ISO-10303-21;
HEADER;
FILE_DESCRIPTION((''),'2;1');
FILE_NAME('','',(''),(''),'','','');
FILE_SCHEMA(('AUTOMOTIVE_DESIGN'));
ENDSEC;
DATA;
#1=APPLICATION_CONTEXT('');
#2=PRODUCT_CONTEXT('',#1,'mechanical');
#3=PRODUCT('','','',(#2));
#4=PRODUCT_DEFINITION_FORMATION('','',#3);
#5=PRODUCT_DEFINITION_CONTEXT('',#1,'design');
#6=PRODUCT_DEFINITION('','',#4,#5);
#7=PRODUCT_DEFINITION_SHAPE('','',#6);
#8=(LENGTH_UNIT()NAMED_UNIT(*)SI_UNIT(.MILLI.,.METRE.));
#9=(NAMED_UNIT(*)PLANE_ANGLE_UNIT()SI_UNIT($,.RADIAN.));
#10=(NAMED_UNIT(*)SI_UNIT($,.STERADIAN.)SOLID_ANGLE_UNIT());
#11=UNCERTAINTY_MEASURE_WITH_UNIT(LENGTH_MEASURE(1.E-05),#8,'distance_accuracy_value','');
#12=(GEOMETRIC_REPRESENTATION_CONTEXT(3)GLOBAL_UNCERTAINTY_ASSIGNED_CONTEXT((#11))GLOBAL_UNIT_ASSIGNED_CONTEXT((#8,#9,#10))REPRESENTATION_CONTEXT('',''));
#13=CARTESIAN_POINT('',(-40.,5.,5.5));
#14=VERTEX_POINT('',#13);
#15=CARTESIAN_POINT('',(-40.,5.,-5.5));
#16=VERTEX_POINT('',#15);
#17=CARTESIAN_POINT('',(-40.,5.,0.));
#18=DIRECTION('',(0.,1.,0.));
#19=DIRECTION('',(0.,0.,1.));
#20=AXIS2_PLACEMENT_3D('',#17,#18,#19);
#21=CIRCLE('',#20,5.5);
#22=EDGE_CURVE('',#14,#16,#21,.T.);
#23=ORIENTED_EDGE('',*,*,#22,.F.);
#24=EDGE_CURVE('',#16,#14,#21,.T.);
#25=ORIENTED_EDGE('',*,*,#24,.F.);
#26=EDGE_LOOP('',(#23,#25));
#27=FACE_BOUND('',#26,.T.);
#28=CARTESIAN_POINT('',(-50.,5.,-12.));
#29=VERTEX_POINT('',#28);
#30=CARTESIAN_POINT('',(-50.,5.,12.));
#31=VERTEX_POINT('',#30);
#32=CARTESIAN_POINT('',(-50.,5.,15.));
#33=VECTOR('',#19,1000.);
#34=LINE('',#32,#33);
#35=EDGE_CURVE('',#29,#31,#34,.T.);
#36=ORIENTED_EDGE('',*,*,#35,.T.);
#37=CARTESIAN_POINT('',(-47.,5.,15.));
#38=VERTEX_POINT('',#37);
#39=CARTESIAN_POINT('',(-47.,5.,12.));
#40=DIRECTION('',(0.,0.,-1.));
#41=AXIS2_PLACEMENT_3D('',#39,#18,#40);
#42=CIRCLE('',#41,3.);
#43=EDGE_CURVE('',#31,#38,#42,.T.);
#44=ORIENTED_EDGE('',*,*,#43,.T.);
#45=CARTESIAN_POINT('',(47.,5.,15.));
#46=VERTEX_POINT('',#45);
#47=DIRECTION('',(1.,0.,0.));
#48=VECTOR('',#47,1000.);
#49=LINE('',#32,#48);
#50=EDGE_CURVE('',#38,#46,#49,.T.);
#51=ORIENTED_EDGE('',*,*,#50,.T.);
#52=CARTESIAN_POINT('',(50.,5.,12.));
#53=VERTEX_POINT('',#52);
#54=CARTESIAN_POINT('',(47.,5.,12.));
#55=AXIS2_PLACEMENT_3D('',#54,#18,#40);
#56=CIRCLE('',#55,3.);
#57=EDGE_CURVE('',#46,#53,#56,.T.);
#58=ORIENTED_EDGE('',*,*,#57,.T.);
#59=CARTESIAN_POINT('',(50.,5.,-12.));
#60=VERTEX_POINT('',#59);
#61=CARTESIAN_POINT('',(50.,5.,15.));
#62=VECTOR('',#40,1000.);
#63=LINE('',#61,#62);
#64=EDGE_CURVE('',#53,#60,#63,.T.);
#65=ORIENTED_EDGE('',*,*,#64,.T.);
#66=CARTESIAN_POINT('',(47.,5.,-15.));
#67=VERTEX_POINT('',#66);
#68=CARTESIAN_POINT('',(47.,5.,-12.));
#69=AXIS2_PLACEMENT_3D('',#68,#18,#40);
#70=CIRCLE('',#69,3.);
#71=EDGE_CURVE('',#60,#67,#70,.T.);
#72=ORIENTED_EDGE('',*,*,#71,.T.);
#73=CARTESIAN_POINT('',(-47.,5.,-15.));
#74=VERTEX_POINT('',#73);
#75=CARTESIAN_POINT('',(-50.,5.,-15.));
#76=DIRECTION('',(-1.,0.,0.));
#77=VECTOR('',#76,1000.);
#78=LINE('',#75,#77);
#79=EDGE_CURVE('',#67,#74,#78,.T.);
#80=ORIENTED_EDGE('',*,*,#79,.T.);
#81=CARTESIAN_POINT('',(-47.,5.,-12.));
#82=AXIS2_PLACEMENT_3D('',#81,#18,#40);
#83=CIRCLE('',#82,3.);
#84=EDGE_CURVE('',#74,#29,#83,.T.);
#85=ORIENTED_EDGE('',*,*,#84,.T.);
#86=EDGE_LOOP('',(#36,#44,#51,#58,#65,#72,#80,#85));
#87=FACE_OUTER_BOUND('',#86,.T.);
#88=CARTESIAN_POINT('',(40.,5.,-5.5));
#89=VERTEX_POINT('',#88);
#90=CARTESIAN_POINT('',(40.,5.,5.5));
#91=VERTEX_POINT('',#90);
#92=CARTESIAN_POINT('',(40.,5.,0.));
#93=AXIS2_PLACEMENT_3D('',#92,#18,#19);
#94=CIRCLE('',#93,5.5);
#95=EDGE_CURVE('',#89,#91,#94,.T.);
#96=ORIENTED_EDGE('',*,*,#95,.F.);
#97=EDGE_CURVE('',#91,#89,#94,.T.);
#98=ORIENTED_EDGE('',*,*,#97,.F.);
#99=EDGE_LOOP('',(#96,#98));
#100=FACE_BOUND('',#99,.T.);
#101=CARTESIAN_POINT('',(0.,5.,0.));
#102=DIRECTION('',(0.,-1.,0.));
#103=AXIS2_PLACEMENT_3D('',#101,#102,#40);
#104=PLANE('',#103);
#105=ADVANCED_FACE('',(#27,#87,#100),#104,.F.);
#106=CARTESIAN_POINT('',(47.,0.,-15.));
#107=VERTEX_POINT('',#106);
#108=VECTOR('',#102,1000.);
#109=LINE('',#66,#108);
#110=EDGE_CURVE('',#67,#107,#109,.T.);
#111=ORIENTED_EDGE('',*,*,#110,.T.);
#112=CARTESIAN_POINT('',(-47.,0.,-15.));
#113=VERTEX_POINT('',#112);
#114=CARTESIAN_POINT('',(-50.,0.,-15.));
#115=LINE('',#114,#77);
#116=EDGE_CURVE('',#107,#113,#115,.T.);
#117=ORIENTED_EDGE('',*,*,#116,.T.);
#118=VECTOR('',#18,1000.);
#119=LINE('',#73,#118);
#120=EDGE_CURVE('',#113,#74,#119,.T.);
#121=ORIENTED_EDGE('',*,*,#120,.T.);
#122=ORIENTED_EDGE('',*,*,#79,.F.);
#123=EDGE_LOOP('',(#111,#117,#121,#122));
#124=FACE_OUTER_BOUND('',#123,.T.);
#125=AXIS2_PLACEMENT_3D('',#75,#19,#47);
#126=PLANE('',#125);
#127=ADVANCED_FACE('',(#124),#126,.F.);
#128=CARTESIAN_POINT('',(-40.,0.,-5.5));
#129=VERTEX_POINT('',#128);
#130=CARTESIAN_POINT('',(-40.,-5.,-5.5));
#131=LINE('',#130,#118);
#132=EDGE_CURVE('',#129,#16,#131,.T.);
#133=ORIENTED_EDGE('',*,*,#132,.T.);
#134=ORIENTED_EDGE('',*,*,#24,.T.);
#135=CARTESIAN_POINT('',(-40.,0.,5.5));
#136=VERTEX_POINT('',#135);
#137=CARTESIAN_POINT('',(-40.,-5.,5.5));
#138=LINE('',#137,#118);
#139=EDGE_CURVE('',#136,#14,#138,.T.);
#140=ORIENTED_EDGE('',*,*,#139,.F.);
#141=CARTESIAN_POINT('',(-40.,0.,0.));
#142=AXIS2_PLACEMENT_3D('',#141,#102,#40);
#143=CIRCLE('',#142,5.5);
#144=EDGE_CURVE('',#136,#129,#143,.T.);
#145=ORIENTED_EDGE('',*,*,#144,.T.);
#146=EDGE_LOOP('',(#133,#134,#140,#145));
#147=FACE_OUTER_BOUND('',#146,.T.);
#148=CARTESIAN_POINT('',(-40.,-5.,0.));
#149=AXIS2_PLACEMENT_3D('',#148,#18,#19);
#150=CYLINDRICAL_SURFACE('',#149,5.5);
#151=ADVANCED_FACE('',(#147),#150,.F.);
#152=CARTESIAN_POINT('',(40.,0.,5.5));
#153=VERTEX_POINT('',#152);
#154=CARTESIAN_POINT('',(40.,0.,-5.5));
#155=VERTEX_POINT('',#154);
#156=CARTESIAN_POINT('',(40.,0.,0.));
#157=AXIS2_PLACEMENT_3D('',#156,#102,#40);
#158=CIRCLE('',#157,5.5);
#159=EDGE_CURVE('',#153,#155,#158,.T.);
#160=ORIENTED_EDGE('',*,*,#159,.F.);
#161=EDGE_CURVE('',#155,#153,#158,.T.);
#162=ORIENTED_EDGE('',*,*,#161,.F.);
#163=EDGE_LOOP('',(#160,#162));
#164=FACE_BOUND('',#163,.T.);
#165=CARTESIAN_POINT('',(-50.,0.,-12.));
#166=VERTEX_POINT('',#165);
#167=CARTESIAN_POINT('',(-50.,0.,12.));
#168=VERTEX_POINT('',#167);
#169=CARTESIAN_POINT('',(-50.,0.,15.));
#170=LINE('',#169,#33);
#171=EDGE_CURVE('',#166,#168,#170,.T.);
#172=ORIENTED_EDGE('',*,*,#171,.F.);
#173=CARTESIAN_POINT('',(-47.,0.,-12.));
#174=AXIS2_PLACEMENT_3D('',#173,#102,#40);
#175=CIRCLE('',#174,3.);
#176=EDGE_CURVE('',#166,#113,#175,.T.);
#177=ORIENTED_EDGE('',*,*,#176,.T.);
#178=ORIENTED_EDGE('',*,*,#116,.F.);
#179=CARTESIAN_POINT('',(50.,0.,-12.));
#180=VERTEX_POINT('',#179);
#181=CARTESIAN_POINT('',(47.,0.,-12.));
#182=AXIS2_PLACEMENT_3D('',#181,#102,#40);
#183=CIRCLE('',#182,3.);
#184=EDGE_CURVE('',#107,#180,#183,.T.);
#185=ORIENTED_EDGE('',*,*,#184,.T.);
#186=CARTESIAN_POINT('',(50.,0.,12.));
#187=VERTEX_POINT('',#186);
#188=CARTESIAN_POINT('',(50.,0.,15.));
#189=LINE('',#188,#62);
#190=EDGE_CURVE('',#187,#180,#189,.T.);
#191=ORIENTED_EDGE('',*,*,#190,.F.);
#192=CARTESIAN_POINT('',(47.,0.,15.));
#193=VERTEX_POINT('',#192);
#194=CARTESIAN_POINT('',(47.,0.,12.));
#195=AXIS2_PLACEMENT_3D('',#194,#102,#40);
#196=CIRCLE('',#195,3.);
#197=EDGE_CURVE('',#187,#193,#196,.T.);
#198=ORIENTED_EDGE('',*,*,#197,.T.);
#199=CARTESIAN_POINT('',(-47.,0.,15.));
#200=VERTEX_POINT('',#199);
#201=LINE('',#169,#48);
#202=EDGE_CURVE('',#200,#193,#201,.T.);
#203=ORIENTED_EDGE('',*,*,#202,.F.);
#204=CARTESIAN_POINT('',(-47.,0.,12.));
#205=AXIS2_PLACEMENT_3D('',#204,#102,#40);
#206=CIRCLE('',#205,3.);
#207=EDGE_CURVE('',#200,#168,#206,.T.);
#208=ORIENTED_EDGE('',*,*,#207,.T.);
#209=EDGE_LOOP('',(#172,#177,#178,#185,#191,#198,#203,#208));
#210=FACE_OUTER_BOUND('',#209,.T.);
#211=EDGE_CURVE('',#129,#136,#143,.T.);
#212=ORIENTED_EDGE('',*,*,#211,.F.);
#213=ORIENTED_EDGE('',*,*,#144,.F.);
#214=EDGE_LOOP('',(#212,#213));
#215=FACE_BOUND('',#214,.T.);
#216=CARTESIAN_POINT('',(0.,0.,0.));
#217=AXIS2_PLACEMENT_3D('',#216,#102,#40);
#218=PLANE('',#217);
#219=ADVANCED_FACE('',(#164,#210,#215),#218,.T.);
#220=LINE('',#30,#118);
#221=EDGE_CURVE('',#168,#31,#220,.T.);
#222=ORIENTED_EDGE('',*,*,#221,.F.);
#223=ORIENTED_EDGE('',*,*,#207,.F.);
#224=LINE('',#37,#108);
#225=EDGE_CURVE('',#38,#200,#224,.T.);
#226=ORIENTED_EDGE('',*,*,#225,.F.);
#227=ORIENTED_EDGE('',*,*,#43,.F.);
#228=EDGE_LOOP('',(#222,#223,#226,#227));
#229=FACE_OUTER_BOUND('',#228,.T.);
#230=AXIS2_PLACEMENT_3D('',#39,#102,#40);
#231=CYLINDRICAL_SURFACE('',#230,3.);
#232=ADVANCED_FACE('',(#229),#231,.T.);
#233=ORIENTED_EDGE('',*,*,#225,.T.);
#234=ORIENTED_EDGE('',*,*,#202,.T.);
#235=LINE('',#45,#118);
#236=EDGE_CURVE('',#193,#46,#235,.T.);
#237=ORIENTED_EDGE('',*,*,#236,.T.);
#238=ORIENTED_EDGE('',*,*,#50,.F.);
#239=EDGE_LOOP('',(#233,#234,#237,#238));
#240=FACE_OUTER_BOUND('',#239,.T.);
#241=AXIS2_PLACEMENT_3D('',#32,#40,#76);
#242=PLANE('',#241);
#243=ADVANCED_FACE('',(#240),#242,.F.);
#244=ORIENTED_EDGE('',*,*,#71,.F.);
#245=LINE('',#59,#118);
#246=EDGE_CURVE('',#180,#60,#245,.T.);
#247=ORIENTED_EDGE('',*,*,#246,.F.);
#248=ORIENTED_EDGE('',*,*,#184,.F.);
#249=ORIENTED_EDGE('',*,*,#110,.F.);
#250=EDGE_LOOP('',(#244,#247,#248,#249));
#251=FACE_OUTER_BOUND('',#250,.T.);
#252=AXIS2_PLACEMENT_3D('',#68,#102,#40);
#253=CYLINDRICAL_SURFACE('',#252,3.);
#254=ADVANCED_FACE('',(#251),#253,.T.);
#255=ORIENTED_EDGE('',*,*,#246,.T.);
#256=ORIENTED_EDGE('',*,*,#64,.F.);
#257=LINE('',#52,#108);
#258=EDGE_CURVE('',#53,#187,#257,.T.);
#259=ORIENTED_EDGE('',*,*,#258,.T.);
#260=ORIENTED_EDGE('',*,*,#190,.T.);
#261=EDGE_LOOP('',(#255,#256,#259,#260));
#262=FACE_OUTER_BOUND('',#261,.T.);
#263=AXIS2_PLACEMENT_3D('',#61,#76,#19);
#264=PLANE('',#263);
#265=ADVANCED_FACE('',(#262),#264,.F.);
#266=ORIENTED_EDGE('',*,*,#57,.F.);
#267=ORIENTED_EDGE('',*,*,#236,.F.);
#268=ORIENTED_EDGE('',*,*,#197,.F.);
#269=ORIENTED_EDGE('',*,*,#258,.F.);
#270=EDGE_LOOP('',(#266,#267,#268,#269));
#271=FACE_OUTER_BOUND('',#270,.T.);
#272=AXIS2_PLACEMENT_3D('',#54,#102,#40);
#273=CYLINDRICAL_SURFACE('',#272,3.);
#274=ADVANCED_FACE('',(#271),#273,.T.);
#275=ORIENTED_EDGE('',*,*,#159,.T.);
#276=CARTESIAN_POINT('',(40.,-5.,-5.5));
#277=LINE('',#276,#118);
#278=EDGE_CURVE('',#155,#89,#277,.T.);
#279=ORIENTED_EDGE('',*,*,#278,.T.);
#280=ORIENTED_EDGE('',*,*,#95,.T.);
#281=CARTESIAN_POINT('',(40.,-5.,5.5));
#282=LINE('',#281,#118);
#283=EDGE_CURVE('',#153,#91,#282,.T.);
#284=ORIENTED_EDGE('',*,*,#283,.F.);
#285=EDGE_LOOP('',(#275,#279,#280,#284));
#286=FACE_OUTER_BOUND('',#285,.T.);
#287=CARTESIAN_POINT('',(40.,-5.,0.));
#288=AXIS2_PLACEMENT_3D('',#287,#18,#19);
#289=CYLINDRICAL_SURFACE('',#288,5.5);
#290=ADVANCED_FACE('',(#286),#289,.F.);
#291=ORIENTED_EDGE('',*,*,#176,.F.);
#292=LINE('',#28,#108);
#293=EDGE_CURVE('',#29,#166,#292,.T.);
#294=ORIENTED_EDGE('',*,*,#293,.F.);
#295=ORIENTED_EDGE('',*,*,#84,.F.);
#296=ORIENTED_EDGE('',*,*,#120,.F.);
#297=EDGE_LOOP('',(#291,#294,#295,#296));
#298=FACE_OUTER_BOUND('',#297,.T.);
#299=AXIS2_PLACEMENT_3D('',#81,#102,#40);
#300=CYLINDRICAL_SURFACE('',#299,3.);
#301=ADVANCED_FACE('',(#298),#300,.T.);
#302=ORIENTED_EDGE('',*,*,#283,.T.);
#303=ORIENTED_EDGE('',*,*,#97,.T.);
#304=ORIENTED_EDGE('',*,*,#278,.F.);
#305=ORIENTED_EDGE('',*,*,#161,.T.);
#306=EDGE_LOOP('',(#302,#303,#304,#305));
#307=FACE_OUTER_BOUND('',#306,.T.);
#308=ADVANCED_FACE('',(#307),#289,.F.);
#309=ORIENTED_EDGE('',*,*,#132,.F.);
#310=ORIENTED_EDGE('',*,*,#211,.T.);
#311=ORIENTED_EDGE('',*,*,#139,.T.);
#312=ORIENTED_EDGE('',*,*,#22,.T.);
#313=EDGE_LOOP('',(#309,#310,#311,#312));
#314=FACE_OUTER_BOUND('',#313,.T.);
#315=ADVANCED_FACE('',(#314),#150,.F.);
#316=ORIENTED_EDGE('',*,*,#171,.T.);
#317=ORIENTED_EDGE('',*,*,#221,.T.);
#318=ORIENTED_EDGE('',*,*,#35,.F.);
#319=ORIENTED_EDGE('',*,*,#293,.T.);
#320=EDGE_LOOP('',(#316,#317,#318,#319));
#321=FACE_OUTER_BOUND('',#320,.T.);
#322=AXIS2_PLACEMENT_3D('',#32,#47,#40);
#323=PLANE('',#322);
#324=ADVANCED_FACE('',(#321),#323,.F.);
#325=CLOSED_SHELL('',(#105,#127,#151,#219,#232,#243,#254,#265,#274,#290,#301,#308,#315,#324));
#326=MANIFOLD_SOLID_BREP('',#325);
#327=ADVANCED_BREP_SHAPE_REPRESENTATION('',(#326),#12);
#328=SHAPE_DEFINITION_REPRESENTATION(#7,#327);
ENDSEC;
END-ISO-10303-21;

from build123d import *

# Parameters (mm, degrees)
SKETCH1_W           = 100
SKETCH1_H           = 30
BOSS_EXTRUDE1_DEPTH = 5
FILLET1_R           = 3
SKETCH3_R           = 5.5
CUT_EXTRUDE1_DEPTH  = 10


with BuildPart() as part:
    # Sketch1 → Boss-Extrude1 (new body)
    with BuildSketch(Plane(origin=(0, 0, 0), x_dir=(1, 0, 0), z_dir=(0, 1, 0))):
        Rectangle(SKETCH1_W, SKETCH1_H)
    extrude(amount=BOSS_EXTRUDE1_DEPTH)

    # Fillet1
    fillet1_edges = [part.edges().sort_by_distance(p)[0] for p in [
        (50, 2.5, 15),
        (-50, 2.5, 15),
        (-50, 2.5, -15),
        (50, 2.5, -15),
    ]]
    fillet(fillet1_edges, radius=FILLET1_R)

    # Sketch3 → Cut-Extrude1 (cut)
    with BuildSketch(Plane(origin=(0, 5, 0), x_dir=(1, 0, 0), z_dir=(0, 1, 0))):
        with Locations(Location((-40, 0, 0), (0, 0, 270))):
            Circle(SKETCH3_R)
        with Locations(Location((40, 0, 0), (0, 0, 270))):
            Circle(SKETCH3_R)
    extrude(amount=-CUT_EXTRUDE1_DEPTH, mode=Mode.SUBTRACT)


solid = part.part
